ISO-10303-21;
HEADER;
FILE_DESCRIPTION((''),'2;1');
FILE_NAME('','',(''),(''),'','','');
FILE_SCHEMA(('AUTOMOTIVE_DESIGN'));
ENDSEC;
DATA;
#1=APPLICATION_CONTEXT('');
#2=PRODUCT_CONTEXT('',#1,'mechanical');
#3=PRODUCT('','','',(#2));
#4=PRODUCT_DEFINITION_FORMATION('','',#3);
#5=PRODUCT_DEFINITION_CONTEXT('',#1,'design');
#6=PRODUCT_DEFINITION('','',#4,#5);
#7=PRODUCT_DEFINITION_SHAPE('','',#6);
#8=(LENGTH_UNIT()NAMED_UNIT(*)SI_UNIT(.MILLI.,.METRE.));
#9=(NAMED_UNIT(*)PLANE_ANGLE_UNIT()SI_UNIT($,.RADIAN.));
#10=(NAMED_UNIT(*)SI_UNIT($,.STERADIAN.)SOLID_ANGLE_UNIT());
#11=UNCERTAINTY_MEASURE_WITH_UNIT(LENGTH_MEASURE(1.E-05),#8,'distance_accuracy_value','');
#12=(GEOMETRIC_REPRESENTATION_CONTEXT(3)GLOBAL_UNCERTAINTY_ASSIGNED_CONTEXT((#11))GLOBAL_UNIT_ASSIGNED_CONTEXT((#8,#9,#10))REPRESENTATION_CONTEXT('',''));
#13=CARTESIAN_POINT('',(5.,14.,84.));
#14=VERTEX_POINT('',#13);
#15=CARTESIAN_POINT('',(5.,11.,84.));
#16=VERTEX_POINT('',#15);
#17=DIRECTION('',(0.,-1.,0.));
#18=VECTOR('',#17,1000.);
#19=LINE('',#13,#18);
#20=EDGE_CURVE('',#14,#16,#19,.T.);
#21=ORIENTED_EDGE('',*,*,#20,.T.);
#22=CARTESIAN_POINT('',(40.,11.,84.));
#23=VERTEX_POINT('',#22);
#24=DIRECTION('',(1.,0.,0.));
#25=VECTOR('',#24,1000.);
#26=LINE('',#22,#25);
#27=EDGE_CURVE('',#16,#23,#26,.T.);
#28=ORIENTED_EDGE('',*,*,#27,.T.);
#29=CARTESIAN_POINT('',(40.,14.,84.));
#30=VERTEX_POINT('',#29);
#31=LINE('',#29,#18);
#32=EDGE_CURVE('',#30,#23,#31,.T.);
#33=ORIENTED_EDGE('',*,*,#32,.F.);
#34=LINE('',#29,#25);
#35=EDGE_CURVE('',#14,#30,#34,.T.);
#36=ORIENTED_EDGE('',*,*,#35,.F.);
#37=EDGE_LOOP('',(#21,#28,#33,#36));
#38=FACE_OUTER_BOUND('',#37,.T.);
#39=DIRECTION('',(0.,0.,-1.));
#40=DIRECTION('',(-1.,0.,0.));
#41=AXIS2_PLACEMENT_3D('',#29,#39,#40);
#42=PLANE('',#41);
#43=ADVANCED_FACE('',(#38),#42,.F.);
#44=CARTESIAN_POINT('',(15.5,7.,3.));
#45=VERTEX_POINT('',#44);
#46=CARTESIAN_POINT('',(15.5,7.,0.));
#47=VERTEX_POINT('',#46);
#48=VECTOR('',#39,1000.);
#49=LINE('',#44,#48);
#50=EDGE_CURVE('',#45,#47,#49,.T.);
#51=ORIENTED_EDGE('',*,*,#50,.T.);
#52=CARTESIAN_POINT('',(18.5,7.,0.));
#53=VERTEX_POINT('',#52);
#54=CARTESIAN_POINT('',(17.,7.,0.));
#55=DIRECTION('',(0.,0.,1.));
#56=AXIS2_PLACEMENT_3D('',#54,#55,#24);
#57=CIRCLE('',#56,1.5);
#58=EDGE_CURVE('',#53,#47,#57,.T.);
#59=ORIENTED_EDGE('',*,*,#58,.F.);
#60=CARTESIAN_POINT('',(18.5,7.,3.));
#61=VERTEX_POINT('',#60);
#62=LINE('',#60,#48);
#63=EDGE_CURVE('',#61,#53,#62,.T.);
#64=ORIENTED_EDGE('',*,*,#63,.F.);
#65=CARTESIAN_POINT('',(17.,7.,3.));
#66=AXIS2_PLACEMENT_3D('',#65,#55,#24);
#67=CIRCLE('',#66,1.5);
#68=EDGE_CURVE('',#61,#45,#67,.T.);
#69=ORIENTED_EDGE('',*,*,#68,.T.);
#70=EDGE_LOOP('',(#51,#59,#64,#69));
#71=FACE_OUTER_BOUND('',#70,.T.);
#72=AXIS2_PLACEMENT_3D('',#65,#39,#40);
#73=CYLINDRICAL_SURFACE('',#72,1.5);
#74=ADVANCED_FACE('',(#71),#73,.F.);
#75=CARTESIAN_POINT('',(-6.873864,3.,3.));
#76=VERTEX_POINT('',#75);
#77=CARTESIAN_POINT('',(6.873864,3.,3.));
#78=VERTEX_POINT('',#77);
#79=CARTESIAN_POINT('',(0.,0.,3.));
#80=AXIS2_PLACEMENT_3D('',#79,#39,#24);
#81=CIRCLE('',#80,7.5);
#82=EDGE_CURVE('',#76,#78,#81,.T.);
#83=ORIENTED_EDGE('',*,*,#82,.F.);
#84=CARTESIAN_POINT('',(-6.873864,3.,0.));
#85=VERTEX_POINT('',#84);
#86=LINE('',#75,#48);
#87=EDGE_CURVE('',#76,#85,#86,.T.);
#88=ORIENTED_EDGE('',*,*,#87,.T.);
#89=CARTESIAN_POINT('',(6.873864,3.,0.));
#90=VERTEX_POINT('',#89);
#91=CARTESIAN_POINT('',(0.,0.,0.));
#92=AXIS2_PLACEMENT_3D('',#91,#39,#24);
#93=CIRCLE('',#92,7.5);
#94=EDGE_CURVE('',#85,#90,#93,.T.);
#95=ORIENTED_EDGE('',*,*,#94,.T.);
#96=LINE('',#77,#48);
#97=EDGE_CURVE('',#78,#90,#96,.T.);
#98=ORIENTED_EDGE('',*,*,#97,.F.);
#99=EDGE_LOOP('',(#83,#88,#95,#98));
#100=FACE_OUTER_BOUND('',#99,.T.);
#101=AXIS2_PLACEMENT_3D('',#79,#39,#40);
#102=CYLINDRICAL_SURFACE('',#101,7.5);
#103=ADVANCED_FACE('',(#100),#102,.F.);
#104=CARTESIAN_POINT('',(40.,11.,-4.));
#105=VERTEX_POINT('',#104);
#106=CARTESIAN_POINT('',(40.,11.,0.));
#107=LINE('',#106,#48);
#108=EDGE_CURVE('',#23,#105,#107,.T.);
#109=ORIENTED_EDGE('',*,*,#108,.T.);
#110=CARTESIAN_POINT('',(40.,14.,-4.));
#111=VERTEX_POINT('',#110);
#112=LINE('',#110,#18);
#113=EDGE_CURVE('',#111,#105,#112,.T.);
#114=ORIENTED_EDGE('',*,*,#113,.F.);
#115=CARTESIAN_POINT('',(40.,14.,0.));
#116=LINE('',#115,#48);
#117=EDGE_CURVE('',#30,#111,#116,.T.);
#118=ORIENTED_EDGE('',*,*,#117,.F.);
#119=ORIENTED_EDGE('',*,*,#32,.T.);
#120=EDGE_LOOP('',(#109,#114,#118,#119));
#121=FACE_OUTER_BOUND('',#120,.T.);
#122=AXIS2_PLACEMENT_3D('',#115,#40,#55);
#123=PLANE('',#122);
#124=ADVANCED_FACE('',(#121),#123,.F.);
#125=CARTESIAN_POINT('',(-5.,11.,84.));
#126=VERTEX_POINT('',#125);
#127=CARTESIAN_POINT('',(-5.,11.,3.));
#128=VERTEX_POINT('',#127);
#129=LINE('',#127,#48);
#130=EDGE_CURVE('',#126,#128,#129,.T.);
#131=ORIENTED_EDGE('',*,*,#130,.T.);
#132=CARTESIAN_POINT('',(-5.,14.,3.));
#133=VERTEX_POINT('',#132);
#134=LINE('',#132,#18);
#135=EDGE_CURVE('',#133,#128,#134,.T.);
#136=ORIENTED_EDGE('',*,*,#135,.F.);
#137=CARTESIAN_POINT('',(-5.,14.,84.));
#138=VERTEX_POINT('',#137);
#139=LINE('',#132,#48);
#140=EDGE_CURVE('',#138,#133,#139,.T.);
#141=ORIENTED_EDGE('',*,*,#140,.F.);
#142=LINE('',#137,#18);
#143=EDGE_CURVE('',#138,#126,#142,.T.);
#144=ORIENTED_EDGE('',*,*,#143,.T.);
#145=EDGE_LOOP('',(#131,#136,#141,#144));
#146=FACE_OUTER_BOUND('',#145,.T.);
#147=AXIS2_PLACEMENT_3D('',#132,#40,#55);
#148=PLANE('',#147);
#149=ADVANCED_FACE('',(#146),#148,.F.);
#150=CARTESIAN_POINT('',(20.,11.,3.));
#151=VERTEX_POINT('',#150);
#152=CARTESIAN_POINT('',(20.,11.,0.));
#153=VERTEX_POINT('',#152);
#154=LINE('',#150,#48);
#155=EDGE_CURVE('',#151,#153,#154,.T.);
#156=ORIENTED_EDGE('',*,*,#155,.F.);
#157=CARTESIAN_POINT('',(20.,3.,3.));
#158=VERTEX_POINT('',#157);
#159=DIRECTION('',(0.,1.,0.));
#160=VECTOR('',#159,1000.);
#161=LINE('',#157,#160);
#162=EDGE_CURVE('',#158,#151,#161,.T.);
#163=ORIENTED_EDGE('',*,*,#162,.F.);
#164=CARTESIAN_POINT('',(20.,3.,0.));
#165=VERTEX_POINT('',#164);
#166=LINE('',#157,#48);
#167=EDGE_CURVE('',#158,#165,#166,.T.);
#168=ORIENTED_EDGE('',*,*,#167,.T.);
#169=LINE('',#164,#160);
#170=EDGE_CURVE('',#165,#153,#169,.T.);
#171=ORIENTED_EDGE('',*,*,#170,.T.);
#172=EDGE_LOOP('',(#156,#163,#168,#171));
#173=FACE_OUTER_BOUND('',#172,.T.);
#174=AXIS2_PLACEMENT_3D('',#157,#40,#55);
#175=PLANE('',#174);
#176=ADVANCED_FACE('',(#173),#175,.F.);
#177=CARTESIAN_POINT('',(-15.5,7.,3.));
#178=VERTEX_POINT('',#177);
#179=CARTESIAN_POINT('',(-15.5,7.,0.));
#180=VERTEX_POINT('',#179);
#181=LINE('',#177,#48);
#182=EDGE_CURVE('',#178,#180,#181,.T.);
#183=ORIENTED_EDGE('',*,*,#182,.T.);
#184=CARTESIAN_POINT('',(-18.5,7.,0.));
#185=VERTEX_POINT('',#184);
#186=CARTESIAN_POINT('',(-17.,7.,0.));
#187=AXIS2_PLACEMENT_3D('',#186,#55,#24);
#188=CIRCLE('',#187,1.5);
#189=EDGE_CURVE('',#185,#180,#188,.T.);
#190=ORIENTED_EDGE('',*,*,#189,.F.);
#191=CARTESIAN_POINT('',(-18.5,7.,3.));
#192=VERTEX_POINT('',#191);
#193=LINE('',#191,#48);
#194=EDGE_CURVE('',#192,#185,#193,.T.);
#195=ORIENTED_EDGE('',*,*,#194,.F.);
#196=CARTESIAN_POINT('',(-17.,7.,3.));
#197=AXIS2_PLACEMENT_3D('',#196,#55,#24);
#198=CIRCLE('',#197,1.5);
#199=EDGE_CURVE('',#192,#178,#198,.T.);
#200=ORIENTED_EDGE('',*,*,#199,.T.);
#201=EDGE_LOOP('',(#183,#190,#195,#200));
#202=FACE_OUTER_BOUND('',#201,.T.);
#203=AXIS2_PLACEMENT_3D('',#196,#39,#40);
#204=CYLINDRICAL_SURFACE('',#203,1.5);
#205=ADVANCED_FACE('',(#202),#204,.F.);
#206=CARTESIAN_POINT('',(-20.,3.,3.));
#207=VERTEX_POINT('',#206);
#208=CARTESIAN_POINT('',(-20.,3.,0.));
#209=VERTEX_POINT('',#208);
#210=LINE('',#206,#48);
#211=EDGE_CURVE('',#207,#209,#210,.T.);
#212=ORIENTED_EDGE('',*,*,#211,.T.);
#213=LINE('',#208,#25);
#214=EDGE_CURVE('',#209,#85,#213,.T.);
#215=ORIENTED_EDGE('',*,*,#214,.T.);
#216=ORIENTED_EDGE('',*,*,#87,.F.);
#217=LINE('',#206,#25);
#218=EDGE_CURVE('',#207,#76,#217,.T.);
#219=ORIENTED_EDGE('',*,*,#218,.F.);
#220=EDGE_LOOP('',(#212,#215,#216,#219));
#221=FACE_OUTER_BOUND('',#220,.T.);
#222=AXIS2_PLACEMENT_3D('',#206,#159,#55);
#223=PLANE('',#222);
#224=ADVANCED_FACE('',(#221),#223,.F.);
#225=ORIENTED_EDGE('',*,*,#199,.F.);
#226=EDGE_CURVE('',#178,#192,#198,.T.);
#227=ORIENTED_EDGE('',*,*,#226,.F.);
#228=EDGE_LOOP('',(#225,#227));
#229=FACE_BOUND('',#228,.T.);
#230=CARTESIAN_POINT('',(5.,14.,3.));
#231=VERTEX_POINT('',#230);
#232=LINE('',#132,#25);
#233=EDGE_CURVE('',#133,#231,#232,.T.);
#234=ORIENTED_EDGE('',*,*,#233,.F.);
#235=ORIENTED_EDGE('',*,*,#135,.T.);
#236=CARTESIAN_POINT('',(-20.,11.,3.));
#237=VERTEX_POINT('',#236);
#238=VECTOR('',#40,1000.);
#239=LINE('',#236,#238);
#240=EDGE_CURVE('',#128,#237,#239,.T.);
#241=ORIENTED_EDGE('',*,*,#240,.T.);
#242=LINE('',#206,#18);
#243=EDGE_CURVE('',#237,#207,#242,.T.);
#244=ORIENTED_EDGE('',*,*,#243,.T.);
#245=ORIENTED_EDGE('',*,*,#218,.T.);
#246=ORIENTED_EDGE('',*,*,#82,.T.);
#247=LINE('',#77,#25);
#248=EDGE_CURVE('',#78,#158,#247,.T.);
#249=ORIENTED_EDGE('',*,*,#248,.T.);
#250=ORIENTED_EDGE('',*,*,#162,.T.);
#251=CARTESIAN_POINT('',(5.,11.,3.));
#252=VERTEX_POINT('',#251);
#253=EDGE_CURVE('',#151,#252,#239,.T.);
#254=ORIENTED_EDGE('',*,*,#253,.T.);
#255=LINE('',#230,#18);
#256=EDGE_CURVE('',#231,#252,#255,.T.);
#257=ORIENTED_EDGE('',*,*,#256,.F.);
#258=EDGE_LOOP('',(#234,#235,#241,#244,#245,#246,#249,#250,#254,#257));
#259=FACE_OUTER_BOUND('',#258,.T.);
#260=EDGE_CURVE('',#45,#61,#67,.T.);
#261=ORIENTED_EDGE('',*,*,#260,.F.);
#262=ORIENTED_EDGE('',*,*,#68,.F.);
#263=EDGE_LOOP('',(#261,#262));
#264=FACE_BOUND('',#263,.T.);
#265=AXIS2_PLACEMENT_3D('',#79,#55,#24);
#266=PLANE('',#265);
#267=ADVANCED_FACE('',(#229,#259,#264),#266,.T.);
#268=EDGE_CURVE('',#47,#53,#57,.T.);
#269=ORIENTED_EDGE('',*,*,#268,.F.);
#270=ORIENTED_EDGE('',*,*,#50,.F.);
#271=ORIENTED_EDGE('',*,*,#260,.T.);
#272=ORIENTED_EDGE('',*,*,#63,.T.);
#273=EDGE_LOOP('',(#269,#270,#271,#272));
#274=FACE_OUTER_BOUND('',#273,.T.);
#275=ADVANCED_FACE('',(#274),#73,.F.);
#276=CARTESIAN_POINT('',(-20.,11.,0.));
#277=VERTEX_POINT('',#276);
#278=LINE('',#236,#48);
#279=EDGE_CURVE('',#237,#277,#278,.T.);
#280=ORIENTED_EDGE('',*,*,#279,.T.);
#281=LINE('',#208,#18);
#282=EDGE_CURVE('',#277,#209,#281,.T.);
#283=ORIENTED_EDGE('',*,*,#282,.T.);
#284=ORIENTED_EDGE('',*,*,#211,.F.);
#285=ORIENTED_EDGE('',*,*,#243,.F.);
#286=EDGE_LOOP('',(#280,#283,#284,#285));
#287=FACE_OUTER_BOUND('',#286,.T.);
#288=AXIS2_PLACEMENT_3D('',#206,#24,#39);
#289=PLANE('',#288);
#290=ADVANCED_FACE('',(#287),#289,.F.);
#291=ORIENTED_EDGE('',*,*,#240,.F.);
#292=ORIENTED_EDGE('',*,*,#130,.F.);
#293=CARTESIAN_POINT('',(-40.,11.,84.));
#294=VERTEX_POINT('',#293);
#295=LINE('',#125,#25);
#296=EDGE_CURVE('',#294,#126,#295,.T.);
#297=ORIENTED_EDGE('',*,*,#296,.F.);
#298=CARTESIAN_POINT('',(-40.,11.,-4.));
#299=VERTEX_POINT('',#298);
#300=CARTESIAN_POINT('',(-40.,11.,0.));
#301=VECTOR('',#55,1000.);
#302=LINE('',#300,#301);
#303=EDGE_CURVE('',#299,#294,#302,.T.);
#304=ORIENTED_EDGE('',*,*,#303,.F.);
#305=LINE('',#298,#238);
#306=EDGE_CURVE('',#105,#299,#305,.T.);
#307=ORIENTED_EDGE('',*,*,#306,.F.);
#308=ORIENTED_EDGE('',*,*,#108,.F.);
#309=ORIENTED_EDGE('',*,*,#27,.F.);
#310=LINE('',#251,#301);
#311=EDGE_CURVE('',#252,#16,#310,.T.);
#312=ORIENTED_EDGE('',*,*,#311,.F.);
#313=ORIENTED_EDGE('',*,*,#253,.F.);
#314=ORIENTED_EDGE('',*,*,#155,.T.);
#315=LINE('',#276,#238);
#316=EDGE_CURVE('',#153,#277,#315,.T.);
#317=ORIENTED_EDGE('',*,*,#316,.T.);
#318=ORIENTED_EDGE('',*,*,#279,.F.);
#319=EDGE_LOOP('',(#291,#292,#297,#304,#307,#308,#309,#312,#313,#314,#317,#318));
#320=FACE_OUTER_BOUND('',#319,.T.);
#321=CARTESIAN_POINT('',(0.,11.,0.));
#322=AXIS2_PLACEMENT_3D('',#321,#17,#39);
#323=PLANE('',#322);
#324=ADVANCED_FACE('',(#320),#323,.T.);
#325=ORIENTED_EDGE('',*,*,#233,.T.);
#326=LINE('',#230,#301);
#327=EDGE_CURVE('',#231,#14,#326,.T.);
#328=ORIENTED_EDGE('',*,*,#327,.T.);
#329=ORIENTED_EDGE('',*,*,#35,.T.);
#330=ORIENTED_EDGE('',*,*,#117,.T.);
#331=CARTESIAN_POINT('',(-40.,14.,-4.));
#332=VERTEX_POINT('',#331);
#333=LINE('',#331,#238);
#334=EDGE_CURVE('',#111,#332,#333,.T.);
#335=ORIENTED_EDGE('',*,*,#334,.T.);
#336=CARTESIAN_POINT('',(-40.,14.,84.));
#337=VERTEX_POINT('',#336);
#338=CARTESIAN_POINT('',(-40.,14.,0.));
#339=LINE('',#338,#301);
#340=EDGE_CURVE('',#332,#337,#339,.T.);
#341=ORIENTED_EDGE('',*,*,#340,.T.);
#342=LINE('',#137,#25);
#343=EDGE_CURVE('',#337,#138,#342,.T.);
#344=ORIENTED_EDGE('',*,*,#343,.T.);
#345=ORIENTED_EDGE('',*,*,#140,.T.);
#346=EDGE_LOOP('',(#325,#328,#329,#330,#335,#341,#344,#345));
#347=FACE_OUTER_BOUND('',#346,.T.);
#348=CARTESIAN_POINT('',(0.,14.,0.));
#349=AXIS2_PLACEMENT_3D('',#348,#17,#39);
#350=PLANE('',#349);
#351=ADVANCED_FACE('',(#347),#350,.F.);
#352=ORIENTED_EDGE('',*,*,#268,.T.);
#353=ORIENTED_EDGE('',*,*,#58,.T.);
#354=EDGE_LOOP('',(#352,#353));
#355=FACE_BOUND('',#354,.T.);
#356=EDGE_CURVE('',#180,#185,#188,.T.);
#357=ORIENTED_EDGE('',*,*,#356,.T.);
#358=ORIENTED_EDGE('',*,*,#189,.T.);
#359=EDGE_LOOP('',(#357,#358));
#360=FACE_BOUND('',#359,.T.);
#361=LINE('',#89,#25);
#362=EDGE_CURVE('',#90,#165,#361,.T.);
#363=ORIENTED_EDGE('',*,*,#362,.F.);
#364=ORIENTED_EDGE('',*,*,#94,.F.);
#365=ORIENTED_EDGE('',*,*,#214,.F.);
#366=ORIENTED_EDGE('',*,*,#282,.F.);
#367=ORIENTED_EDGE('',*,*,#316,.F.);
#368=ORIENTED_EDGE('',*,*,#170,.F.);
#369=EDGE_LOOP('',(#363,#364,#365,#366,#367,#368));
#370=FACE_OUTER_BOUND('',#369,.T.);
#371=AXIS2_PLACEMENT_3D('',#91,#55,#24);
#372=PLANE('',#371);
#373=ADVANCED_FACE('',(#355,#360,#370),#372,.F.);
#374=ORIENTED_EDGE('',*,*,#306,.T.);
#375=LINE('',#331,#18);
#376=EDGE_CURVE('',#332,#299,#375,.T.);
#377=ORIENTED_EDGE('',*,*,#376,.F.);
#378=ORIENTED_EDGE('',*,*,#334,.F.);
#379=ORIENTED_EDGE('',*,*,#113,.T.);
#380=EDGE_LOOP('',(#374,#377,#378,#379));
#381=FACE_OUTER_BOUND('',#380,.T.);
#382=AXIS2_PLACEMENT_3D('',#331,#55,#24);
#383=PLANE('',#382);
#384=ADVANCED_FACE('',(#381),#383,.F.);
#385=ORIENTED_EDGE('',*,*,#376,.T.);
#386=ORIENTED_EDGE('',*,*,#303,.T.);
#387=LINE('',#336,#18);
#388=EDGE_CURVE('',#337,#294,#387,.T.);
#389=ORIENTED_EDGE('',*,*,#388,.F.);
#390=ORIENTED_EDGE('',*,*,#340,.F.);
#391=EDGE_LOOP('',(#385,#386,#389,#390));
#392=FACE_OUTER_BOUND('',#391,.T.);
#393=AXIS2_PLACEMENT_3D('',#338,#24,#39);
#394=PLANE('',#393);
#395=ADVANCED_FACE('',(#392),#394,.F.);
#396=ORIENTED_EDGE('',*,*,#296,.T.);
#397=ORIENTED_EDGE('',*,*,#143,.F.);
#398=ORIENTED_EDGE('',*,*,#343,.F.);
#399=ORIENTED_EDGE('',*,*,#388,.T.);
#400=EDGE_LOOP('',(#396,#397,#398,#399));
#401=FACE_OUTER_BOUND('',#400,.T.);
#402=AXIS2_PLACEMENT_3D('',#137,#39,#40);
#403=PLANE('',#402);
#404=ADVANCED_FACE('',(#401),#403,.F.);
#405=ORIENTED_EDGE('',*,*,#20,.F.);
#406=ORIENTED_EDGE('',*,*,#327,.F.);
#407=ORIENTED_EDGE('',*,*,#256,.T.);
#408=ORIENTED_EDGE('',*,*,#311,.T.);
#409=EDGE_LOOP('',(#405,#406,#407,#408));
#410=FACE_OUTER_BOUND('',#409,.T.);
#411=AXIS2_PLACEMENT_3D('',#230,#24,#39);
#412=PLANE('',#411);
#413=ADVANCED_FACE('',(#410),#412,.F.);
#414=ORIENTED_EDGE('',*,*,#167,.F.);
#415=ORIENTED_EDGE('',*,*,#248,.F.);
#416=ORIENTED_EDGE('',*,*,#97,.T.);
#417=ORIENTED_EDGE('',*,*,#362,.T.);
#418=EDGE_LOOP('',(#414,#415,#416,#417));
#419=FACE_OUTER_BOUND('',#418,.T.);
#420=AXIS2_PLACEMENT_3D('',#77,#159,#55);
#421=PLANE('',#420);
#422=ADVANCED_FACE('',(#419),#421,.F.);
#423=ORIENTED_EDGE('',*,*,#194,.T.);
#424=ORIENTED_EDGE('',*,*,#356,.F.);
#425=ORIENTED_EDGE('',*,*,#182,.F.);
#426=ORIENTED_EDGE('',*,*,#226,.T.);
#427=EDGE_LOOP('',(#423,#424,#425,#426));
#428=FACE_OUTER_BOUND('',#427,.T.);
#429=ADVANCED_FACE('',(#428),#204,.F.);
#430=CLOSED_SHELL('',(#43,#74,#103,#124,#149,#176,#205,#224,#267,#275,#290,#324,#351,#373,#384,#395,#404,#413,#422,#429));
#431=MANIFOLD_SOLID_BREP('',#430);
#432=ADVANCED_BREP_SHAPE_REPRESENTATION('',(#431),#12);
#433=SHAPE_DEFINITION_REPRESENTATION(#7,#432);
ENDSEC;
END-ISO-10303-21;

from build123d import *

# Parameters (mm, degrees)
SKETCH2_R           = 1.5
BOSS_EXTRUDE1_DEPTH = 3
BOSS_EXTRUDE2_DEPTH = 3


with BuildPart() as part:
    # Sketch2 → Boss-Extrude1 (new body)
    with BuildSketch(Plane.XY):
        with BuildLine():
            Line((-20, 3), (-6.873863542, 3))
            ThreePointArc((-6.873863542, 3), (0, 7.5), (6.873863542, 3))
            Line((6.873863542, 3), (20, 3))
            Line((20, 3), (20, 11))
            Line((20, 11), (-20, 11))
            Line((-20, 11), (-20, 3))
        make_face()
        with Locations((-17, 7)):
            Circle(SKETCH2_R, mode=Mode.SUBTRACT)
        with Locations((17, 7)):
            Circle(SKETCH2_R, mode=Mode.SUBTRACT)
    extrude(amount=BOSS_EXTRUDE1_DEPTH)

    # Sketch3 → Boss-Extrude2 (add)
    with BuildSketch(Plane(origin=(0, 11, 0), x_dir=(1, 0, 0), z_dir=(0, 1, 0))):
        Polygon((-5, -84), (-40, -84), (-40, 0), (-40, 4), (40, 4), (40, 0), (40, -84), (5, -84), (5, -3), (-5, -3), align=None)
    extrude(amount=BOSS_EXTRUDE2_DEPTH)


solid = part.part
